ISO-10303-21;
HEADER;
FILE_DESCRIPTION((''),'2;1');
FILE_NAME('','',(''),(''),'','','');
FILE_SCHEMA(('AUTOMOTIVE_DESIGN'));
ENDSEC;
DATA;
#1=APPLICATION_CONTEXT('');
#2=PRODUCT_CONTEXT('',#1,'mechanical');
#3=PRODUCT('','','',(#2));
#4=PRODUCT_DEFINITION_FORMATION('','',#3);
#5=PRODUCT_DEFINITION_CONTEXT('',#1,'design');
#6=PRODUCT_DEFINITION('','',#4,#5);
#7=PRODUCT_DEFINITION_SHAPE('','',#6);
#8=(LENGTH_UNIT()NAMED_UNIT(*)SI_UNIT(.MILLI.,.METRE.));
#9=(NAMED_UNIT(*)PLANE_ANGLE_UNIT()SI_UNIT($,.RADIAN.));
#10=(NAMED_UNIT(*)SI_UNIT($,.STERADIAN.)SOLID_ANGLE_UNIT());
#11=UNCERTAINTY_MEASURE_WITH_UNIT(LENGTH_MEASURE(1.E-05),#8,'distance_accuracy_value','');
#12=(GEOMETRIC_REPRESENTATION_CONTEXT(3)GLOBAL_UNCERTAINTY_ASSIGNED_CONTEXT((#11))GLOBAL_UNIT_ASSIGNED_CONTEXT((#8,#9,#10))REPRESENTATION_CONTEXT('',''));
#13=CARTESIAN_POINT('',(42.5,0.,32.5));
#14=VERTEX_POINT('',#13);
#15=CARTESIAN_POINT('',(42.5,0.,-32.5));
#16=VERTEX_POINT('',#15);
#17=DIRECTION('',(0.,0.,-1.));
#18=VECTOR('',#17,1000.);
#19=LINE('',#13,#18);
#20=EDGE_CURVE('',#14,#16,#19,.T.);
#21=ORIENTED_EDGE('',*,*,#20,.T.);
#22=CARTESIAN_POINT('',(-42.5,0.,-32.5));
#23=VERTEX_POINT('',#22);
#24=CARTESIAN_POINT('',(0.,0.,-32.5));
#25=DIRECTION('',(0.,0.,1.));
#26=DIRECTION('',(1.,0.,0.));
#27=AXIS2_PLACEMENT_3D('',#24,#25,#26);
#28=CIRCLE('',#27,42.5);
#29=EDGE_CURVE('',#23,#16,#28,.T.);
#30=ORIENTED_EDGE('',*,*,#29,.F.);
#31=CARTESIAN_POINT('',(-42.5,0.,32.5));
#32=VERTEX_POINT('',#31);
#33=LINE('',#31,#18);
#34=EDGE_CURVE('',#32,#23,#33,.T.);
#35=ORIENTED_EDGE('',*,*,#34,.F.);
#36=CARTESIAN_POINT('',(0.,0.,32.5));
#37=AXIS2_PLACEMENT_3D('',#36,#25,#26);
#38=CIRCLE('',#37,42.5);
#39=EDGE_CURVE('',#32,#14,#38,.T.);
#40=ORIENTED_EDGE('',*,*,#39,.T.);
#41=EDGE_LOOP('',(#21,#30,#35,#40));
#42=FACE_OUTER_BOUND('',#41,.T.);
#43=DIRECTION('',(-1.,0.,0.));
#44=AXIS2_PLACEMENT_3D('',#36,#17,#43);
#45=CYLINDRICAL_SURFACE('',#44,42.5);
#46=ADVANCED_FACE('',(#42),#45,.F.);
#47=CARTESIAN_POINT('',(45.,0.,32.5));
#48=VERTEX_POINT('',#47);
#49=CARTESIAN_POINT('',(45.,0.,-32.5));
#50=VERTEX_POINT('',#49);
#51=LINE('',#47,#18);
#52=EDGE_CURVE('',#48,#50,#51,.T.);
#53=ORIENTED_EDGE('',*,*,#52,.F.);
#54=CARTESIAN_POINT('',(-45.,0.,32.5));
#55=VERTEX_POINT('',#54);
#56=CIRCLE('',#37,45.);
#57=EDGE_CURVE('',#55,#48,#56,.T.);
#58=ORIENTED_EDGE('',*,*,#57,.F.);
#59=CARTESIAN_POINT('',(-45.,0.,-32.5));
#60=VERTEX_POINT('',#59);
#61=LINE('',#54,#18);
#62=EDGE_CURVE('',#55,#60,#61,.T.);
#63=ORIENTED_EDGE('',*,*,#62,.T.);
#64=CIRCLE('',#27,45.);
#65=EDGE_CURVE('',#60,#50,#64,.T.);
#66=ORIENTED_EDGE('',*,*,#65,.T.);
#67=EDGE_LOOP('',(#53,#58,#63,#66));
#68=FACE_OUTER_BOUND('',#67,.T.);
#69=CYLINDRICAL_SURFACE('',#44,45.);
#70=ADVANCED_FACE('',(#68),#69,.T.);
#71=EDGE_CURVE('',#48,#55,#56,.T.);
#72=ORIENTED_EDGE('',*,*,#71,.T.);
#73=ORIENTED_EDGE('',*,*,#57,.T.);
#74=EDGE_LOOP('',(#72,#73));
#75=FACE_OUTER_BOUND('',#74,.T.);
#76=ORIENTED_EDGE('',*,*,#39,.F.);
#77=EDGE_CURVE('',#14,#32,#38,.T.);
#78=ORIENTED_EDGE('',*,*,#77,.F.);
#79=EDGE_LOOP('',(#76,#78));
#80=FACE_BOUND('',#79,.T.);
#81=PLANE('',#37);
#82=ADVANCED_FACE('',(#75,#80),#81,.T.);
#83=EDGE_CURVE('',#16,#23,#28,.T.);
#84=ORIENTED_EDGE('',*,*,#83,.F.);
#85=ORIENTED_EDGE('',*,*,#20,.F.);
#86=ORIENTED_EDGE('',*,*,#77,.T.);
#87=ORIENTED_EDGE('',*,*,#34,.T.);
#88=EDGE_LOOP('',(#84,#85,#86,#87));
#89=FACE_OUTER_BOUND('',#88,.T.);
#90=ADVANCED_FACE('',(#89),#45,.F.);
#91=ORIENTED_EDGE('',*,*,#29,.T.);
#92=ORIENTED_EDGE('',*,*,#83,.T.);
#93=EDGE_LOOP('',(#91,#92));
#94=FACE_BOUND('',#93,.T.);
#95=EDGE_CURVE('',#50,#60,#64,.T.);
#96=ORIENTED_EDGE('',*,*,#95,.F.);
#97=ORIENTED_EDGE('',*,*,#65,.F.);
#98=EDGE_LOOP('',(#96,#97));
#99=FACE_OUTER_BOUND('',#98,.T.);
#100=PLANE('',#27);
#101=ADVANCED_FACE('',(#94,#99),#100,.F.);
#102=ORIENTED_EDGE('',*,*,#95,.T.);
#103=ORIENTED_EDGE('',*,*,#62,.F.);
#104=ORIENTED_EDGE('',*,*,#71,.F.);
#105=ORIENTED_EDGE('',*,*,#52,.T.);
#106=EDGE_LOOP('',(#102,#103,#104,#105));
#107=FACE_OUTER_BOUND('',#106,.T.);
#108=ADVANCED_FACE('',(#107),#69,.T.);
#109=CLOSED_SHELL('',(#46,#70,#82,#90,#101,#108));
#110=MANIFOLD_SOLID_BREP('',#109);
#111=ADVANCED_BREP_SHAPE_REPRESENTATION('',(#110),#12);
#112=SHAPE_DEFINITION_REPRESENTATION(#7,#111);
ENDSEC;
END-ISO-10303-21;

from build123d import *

# Parameters (mm, degrees)
SKETCH_1_R      = 45
SKETCH_1_R_2    = 42.5
EXTRUDE_1_DEPTH = 32.5


with BuildPart() as part:
    # 草图1 → 凸台-拉伸1 (new, symmetric)
    with BuildSketch(Plane.XY):
        Circle(SKETCH_1_R)
        Circle(SKETCH_1_R_2, mode=Mode.SUBTRACT)
    extrude(amount=EXTRUDE_1_DEPTH, both=True)


solid = part.part
